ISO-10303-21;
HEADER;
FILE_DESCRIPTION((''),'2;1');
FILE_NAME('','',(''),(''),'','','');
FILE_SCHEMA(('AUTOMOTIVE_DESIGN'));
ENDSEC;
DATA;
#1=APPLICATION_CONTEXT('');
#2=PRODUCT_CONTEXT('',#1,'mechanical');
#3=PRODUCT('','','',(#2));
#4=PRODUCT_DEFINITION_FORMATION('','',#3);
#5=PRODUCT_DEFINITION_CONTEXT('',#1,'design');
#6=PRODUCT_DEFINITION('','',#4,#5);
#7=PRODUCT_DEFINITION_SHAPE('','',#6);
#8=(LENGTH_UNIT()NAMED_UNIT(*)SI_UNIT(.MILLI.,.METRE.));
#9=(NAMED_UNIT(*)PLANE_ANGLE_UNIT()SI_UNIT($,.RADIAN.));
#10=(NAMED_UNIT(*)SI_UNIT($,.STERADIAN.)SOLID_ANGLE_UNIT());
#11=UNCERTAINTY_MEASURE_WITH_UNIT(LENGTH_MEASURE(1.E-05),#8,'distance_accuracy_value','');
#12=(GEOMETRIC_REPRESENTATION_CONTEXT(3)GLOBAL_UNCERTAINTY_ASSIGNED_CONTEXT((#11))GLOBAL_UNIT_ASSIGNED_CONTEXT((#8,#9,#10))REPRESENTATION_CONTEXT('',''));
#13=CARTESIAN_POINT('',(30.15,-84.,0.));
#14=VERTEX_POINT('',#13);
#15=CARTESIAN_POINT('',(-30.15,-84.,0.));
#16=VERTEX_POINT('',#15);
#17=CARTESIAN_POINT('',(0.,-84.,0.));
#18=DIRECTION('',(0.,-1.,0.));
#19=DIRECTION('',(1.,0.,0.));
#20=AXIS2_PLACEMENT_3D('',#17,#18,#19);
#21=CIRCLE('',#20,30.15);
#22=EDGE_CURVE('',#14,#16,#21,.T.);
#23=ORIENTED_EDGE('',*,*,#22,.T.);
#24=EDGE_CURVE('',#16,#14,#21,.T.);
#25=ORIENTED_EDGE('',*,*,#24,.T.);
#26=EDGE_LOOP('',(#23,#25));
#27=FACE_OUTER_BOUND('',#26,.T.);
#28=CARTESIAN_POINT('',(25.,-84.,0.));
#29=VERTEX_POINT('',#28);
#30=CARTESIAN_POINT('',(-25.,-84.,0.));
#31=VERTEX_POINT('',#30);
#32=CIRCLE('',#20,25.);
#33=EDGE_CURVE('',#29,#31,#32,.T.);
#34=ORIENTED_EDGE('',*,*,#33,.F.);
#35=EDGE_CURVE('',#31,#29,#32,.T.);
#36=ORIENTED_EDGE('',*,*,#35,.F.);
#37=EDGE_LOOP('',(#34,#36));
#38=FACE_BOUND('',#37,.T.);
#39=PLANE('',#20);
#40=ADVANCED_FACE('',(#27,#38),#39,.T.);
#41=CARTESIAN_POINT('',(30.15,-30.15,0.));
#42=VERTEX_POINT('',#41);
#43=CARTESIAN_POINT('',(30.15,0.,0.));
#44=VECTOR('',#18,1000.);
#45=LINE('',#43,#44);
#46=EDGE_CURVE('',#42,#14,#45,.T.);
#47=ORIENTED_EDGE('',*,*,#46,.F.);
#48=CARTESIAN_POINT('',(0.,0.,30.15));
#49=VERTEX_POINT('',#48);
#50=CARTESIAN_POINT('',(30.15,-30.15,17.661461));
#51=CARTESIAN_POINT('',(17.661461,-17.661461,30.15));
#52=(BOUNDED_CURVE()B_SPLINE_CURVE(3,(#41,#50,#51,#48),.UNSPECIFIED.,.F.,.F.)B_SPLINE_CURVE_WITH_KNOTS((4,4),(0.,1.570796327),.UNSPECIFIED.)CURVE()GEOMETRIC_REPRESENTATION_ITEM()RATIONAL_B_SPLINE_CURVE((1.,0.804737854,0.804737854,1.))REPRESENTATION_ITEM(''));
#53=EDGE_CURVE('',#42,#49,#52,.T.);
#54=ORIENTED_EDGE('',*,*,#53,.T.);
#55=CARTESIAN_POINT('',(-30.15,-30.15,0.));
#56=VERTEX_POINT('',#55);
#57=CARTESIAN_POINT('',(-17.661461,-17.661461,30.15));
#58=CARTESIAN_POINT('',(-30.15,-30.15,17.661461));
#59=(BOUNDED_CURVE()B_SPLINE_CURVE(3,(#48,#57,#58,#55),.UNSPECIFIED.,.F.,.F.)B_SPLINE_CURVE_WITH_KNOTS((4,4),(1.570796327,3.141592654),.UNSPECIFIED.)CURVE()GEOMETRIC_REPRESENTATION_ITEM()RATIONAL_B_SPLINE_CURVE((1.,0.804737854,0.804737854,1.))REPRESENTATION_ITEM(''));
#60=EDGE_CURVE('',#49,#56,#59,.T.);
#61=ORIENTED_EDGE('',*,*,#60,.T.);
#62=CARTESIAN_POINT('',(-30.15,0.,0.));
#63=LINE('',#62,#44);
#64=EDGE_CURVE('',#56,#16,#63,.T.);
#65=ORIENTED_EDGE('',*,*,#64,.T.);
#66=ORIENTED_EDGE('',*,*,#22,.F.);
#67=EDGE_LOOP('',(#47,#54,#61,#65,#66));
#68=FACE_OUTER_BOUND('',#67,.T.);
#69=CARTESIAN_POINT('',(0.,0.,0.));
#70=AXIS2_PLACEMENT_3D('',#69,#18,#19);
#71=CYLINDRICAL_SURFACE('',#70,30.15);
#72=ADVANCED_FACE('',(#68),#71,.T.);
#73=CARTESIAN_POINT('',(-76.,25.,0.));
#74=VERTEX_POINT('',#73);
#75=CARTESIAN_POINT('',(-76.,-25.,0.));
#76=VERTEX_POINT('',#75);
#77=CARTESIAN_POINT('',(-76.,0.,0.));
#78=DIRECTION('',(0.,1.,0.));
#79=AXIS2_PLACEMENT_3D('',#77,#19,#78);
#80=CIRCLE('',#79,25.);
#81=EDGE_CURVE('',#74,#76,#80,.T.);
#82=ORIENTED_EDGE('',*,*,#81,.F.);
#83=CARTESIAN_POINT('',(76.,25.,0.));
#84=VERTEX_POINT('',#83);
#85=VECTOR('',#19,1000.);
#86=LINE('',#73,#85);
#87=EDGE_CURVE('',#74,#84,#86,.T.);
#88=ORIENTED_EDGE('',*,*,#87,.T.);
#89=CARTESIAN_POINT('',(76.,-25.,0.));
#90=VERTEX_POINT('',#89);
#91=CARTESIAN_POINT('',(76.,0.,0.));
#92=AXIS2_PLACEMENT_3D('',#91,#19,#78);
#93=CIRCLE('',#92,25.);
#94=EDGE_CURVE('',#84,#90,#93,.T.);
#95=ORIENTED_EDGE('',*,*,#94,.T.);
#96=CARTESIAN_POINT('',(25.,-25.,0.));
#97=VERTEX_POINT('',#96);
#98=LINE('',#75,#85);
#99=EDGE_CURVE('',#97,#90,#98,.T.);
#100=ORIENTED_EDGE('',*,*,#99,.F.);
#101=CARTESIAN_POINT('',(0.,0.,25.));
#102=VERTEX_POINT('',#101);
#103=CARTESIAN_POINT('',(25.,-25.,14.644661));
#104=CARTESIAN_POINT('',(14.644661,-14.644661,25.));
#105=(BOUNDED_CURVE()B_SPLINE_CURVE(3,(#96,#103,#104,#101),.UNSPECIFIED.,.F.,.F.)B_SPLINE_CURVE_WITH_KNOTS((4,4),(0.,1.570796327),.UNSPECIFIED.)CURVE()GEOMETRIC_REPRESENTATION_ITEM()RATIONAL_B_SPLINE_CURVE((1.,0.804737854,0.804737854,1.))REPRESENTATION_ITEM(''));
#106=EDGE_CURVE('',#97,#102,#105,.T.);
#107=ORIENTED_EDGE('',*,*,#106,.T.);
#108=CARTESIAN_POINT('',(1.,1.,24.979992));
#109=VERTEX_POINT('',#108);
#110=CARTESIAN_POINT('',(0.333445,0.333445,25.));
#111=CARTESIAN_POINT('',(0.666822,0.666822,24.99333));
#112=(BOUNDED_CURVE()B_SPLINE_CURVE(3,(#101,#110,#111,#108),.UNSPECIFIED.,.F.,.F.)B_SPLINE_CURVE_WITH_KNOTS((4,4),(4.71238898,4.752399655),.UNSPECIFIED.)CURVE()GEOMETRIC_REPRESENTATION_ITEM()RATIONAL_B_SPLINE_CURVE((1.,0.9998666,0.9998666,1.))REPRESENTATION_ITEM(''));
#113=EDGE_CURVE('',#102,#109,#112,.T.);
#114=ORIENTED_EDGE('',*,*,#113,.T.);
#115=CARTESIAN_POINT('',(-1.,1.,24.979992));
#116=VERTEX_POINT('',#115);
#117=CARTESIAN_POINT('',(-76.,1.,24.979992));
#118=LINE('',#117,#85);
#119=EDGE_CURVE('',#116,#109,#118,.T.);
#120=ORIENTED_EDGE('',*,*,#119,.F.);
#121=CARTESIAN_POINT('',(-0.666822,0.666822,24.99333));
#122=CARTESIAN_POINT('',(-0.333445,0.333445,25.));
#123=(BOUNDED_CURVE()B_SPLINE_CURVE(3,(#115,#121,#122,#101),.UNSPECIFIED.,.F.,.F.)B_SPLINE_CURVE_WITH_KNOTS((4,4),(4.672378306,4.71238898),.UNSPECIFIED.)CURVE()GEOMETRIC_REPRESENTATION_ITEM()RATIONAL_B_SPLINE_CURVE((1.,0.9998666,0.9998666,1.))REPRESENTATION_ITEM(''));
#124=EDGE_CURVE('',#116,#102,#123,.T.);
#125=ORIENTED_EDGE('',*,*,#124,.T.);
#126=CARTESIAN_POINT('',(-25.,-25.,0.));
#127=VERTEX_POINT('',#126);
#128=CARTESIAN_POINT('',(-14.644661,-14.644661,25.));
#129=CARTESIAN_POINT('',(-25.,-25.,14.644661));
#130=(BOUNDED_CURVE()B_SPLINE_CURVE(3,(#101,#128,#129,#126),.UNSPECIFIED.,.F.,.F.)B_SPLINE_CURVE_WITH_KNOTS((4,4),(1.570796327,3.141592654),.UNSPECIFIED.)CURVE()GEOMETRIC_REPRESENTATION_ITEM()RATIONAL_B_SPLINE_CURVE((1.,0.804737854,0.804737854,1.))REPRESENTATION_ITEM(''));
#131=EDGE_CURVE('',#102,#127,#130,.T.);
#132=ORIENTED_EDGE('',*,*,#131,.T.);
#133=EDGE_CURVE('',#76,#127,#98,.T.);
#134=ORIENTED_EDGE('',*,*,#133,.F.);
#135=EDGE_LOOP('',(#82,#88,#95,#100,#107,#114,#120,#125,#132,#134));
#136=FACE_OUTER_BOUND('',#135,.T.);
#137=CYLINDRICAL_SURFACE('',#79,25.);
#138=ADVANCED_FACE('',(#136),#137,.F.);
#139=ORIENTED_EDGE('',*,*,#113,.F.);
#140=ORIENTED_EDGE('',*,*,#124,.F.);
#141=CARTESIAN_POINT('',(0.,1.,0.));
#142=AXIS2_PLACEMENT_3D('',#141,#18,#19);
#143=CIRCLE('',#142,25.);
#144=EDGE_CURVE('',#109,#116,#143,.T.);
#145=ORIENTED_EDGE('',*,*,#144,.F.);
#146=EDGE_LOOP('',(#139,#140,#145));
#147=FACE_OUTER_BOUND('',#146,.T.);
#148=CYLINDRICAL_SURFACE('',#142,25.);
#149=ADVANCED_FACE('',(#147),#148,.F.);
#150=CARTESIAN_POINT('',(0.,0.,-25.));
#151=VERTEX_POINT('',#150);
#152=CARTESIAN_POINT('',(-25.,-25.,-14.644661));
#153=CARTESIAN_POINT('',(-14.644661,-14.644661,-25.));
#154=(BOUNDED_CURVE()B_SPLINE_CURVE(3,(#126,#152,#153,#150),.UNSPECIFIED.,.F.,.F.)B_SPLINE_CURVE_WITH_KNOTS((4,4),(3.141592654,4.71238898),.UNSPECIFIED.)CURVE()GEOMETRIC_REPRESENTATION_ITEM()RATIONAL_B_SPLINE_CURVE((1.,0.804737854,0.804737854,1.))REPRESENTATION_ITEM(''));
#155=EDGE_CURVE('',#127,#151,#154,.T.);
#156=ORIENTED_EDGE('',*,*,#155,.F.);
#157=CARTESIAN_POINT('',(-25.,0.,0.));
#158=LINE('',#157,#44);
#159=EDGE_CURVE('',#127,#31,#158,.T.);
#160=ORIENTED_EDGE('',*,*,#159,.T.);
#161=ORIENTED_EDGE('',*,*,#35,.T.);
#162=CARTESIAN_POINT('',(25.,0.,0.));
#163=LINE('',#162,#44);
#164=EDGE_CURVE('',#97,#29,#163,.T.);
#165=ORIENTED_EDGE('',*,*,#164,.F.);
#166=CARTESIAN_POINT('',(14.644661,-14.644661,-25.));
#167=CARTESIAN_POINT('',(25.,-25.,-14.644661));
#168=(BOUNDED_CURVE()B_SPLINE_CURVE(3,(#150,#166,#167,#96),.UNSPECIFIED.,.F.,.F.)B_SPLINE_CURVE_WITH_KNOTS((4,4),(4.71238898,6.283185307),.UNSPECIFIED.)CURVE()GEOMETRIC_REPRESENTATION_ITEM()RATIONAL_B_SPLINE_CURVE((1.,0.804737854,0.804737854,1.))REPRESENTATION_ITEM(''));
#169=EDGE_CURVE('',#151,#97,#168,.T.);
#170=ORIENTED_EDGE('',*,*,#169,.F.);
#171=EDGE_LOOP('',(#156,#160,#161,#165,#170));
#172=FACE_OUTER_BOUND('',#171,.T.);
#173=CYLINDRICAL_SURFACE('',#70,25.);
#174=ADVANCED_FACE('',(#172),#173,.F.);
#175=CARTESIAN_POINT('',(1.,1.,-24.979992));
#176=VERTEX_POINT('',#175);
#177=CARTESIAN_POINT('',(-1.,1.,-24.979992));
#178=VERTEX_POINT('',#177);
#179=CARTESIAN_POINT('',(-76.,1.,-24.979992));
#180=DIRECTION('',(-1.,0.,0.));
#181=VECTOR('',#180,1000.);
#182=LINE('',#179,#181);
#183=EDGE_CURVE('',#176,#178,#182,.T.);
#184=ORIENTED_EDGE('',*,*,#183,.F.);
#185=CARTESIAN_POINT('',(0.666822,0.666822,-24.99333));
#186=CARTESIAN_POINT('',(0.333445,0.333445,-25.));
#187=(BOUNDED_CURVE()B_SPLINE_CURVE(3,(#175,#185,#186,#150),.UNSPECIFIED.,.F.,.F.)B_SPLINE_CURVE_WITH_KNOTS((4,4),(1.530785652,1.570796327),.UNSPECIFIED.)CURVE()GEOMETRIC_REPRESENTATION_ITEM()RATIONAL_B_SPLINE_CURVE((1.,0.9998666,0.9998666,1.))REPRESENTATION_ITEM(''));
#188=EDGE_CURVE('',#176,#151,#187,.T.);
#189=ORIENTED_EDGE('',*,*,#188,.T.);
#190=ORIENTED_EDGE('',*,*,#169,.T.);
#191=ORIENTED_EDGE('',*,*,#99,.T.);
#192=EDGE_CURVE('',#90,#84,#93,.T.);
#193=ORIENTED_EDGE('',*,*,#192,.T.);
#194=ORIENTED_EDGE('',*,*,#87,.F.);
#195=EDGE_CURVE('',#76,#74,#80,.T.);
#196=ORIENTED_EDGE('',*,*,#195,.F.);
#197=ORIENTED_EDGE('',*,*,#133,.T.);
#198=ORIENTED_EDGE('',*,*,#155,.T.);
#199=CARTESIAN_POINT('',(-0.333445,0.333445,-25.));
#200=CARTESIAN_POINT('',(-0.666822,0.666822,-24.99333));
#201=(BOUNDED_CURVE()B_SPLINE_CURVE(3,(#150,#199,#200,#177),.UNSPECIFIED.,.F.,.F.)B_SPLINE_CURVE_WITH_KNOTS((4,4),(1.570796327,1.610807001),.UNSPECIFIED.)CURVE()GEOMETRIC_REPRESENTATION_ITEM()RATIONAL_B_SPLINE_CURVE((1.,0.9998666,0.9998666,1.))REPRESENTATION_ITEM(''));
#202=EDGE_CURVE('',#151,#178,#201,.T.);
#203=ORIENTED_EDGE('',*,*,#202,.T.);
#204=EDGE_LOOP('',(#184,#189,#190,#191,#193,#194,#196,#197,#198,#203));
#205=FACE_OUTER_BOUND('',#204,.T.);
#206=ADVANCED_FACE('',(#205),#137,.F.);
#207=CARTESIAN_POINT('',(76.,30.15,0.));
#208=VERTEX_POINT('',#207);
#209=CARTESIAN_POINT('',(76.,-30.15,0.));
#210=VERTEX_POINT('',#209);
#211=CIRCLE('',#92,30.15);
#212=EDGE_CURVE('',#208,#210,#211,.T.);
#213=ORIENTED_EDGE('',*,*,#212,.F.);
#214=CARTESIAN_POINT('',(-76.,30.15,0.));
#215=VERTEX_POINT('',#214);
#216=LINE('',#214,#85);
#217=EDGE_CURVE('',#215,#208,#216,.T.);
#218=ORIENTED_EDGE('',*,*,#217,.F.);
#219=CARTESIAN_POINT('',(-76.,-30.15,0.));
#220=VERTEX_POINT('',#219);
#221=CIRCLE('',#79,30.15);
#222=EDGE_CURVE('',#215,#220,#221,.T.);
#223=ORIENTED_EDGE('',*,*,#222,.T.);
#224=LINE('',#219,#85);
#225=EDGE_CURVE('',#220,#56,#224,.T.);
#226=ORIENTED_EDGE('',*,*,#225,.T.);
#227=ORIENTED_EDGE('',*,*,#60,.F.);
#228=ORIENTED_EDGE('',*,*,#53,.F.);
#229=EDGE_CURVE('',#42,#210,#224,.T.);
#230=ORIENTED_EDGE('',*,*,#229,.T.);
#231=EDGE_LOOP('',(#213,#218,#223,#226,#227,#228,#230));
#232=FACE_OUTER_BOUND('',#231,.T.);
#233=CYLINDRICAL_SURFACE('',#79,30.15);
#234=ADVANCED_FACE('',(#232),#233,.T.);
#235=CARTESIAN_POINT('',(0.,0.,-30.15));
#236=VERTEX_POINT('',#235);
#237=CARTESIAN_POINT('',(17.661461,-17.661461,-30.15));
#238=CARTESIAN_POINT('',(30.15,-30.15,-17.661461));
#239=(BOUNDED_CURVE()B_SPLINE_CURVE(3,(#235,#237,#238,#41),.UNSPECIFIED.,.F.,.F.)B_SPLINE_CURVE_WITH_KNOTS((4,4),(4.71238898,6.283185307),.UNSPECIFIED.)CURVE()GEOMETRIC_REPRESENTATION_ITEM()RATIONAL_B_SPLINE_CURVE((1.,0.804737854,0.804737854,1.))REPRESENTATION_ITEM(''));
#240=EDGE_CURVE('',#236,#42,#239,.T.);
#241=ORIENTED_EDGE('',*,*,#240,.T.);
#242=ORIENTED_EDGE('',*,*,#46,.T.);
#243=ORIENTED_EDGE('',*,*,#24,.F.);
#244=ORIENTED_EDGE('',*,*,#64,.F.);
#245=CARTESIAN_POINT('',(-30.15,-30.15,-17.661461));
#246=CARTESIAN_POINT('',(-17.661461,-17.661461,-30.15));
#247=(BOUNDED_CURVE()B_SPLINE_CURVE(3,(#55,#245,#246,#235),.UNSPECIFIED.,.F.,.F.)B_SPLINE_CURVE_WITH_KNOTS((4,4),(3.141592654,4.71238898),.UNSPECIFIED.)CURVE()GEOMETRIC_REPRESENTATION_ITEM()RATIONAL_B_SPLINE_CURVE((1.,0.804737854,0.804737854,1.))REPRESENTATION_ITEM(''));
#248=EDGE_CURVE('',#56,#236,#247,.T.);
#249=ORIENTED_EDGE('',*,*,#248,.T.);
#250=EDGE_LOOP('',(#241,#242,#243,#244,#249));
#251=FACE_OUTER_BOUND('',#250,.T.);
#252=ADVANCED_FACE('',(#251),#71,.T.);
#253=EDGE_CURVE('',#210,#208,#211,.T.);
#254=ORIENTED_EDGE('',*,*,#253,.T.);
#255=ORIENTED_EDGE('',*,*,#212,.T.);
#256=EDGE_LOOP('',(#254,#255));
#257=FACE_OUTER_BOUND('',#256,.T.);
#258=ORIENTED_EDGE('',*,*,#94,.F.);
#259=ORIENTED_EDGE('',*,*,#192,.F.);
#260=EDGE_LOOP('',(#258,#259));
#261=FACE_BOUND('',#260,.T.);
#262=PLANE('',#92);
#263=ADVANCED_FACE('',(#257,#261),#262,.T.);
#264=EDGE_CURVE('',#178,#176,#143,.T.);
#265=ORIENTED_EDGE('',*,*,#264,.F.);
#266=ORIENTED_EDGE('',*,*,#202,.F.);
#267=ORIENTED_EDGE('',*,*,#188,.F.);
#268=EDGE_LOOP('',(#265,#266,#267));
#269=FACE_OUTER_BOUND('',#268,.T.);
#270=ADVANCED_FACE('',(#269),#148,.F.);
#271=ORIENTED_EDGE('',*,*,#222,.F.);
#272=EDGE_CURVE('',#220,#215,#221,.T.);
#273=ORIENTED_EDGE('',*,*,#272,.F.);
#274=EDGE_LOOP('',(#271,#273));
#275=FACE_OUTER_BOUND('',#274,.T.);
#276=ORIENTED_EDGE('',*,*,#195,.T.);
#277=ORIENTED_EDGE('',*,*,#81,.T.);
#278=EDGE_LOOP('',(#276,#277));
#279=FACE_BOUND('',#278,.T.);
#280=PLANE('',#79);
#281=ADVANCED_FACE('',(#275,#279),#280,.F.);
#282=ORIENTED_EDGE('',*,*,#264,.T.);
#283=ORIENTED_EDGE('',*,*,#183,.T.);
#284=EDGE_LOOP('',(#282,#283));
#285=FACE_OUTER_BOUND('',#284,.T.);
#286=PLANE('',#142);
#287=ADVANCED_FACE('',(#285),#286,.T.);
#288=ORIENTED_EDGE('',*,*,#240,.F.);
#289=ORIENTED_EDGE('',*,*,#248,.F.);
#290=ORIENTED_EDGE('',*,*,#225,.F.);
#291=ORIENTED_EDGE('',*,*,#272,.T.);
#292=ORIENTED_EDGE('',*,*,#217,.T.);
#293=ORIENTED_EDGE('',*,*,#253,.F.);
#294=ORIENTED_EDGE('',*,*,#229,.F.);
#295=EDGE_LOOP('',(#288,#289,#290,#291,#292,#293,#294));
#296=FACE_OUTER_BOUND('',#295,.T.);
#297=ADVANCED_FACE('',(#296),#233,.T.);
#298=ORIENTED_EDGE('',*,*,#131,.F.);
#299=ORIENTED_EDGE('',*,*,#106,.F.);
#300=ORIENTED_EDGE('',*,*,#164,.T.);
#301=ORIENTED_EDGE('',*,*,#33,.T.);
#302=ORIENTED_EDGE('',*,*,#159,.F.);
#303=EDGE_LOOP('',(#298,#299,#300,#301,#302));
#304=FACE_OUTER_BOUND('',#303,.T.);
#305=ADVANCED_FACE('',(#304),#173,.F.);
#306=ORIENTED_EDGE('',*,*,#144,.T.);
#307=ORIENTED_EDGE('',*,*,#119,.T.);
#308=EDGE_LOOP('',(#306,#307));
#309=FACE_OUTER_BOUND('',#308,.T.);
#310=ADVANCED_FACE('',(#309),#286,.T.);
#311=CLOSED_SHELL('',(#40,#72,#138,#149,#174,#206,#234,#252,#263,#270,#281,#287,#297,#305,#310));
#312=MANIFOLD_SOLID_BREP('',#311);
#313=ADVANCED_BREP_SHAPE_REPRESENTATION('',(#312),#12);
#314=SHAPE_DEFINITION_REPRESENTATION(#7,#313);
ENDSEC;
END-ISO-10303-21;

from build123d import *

# Parameters (mm, degrees)
SWEEP_THIN_PART_1_PROFILE_R   = 30.15
SWEEP_THIN_PART_1_PROFILE_R_2 = 25
SWEEP_THIN_PART_2_PROFILE_R   = 30.15
SWEEP_THIN_PART_2_PROFILE_R_2 = 25
SKETCH15_R                    = 25
CUT_EXTRUDE1_DEPTH            = 177.264070494
SKETCH18_R                    = 25
CUT_EXTRUDE2_DEPTH            = 85


with BuildPart() as part:
    # Sweep-thin part 1: sweep along a path in Sketch1
    with BuildLine(Plane.XY) as sweep_thin_part_1_path:
        Line((-76, 0), (76, 0))
    # Sweep-thin part 1 profile (on start of the path) → Sweep-thin part 1 (sweep)
    with BuildSketch(Plane.YZ.offset(-76)):
        Circle(SWEEP_THIN_PART_1_PROFILE_R)
        Circle(SWEEP_THIN_PART_1_PROFILE_R_2, mode=Mode.SUBTRACT)
    sweep(path=sweep_thin_part_1_path.line)

    # Sweep-thin part 2: sweep along a path in Sketch8
    with BuildLine(Plane.XY) as sweep_thin_part_2_path:
        Line((0, 0), (0, -84))
    # Sweep-thin part 2 profile (on start of the path) → Sweep-thin part 2 (sweep)
    with BuildSketch(Plane(origin=(0, 0, 0), x_dir=(-1, 0, 0), z_dir=(0, -1, 0))):
        Circle(SWEEP_THIN_PART_2_PROFILE_R)
        Circle(SWEEP_THIN_PART_2_PROFILE_R_2, mode=Mode.SUBTRACT)
    sweep(path=sweep_thin_part_2_path.line)

    # Sketch15 → Cut-Extrude1 (cut, through all)
    with BuildSketch(Plane.ZY.offset(76)):
        with Locations(Location((0, 0, 0), (0, 0, 90))):
            Circle(SKETCH15_R)
    extrude(amount=-CUT_EXTRUDE1_DEPTH, mode=Mode.SUBTRACT)

    # Sketch18 → Cut-Extrude2 (cut)
    with BuildSketch(Plane.XZ.offset(84)):
        Circle(SKETCH18_R)
    extrude(amount=-CUT_EXTRUDE2_DEPTH, mode=Mode.SUBTRACT)


solid = part.part
